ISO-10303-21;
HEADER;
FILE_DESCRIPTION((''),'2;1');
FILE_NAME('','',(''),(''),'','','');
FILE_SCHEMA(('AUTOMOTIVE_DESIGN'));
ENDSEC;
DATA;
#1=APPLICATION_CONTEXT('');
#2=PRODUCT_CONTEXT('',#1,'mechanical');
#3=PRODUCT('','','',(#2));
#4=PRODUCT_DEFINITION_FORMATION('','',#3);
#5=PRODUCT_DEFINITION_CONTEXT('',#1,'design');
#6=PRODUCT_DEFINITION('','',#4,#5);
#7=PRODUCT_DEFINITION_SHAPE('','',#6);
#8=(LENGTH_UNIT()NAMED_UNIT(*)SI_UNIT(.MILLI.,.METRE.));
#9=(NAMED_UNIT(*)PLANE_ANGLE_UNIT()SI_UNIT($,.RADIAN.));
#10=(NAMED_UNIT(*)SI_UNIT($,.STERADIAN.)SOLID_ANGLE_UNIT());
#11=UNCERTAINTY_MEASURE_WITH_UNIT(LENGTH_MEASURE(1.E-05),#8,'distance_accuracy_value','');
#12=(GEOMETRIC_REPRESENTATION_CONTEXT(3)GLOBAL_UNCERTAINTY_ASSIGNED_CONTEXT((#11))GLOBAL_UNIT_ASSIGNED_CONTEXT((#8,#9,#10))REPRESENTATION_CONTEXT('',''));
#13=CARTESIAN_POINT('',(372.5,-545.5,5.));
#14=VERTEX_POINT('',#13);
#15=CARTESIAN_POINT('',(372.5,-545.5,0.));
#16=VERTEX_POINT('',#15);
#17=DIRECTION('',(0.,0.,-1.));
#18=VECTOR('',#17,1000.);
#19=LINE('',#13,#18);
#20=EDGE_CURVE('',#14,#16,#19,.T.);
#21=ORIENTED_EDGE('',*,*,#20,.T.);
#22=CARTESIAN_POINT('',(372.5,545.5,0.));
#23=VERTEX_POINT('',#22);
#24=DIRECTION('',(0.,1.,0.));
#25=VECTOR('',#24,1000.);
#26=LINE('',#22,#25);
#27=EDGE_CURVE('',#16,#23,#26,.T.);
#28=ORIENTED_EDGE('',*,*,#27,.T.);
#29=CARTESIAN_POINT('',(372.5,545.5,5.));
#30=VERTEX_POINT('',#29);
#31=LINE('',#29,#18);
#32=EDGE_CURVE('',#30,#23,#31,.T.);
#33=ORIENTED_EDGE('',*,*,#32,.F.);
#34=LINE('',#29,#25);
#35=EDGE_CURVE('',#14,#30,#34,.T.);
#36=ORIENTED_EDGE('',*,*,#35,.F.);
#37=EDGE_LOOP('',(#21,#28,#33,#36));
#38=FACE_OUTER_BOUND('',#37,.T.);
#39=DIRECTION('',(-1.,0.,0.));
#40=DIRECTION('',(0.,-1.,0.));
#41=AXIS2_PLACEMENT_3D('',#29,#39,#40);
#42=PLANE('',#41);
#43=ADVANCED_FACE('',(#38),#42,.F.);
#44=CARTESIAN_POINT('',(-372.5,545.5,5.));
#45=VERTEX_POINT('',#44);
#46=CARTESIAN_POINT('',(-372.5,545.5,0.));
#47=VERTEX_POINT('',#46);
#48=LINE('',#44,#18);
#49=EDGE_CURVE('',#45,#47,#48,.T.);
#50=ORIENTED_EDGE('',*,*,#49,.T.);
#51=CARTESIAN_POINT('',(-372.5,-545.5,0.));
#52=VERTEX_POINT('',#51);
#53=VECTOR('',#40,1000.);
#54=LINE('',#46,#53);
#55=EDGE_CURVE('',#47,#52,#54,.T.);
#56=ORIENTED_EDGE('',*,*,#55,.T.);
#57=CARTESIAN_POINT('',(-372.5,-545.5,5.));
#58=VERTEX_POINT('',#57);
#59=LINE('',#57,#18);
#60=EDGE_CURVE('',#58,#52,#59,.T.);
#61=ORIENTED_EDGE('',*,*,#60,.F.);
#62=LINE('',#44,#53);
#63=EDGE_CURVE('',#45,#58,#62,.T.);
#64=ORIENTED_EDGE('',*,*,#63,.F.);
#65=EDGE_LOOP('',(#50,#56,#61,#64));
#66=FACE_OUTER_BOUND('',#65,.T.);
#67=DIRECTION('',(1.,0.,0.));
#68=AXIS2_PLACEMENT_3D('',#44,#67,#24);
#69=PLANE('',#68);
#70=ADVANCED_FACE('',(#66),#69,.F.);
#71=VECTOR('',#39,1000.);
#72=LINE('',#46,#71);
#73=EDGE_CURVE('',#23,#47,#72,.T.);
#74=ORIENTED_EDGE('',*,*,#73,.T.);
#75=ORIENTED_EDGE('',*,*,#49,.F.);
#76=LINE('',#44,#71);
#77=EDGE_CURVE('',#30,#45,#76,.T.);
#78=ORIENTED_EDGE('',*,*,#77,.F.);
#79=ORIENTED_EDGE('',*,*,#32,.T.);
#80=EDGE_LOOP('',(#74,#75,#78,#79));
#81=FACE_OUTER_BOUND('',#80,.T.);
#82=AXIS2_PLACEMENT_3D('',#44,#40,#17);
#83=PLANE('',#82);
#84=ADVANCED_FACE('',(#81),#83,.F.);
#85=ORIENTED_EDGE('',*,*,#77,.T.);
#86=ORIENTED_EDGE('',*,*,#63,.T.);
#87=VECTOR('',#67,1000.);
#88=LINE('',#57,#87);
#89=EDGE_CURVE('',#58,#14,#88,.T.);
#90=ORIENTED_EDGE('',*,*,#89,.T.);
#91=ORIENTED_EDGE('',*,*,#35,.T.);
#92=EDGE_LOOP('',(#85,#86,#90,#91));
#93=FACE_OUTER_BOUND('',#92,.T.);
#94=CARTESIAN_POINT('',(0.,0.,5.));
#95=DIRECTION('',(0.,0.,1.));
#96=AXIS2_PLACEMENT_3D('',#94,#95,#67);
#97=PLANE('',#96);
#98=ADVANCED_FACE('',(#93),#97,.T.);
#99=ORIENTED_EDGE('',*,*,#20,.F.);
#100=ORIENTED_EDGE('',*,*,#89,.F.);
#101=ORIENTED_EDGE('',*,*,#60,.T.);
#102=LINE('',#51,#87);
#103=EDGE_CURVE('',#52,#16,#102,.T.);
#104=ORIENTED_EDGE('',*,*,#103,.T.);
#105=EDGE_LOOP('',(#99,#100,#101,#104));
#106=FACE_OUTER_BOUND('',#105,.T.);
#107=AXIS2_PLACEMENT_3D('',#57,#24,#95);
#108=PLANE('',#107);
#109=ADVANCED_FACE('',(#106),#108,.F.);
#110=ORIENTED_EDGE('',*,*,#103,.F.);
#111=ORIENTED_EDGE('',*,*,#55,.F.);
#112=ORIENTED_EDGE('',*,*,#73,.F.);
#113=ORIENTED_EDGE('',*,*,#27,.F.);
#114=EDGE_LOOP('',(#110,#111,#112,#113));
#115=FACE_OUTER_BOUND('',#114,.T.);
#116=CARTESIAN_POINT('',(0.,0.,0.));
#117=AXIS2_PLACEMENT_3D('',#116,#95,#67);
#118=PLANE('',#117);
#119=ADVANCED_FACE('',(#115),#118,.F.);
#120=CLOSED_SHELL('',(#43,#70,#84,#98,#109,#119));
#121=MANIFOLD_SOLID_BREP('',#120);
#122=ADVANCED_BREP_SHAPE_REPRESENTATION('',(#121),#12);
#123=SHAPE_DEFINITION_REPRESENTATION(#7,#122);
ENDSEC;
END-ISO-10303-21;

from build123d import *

# Parameters (mm, degrees)
SKETCH_1_W      = 745
SKETCH_1_H      = 1091
EXTRUDE_1_DEPTH = 5


with BuildPart() as part:
    # 草图1 → 凸台-拉伸1 (new body)
    with BuildSketch(Plane.XY):
        Rectangle(SKETCH_1_W, SKETCH_1_H)
    extrude(amount=EXTRUDE_1_DEPTH)


solid = part.part
